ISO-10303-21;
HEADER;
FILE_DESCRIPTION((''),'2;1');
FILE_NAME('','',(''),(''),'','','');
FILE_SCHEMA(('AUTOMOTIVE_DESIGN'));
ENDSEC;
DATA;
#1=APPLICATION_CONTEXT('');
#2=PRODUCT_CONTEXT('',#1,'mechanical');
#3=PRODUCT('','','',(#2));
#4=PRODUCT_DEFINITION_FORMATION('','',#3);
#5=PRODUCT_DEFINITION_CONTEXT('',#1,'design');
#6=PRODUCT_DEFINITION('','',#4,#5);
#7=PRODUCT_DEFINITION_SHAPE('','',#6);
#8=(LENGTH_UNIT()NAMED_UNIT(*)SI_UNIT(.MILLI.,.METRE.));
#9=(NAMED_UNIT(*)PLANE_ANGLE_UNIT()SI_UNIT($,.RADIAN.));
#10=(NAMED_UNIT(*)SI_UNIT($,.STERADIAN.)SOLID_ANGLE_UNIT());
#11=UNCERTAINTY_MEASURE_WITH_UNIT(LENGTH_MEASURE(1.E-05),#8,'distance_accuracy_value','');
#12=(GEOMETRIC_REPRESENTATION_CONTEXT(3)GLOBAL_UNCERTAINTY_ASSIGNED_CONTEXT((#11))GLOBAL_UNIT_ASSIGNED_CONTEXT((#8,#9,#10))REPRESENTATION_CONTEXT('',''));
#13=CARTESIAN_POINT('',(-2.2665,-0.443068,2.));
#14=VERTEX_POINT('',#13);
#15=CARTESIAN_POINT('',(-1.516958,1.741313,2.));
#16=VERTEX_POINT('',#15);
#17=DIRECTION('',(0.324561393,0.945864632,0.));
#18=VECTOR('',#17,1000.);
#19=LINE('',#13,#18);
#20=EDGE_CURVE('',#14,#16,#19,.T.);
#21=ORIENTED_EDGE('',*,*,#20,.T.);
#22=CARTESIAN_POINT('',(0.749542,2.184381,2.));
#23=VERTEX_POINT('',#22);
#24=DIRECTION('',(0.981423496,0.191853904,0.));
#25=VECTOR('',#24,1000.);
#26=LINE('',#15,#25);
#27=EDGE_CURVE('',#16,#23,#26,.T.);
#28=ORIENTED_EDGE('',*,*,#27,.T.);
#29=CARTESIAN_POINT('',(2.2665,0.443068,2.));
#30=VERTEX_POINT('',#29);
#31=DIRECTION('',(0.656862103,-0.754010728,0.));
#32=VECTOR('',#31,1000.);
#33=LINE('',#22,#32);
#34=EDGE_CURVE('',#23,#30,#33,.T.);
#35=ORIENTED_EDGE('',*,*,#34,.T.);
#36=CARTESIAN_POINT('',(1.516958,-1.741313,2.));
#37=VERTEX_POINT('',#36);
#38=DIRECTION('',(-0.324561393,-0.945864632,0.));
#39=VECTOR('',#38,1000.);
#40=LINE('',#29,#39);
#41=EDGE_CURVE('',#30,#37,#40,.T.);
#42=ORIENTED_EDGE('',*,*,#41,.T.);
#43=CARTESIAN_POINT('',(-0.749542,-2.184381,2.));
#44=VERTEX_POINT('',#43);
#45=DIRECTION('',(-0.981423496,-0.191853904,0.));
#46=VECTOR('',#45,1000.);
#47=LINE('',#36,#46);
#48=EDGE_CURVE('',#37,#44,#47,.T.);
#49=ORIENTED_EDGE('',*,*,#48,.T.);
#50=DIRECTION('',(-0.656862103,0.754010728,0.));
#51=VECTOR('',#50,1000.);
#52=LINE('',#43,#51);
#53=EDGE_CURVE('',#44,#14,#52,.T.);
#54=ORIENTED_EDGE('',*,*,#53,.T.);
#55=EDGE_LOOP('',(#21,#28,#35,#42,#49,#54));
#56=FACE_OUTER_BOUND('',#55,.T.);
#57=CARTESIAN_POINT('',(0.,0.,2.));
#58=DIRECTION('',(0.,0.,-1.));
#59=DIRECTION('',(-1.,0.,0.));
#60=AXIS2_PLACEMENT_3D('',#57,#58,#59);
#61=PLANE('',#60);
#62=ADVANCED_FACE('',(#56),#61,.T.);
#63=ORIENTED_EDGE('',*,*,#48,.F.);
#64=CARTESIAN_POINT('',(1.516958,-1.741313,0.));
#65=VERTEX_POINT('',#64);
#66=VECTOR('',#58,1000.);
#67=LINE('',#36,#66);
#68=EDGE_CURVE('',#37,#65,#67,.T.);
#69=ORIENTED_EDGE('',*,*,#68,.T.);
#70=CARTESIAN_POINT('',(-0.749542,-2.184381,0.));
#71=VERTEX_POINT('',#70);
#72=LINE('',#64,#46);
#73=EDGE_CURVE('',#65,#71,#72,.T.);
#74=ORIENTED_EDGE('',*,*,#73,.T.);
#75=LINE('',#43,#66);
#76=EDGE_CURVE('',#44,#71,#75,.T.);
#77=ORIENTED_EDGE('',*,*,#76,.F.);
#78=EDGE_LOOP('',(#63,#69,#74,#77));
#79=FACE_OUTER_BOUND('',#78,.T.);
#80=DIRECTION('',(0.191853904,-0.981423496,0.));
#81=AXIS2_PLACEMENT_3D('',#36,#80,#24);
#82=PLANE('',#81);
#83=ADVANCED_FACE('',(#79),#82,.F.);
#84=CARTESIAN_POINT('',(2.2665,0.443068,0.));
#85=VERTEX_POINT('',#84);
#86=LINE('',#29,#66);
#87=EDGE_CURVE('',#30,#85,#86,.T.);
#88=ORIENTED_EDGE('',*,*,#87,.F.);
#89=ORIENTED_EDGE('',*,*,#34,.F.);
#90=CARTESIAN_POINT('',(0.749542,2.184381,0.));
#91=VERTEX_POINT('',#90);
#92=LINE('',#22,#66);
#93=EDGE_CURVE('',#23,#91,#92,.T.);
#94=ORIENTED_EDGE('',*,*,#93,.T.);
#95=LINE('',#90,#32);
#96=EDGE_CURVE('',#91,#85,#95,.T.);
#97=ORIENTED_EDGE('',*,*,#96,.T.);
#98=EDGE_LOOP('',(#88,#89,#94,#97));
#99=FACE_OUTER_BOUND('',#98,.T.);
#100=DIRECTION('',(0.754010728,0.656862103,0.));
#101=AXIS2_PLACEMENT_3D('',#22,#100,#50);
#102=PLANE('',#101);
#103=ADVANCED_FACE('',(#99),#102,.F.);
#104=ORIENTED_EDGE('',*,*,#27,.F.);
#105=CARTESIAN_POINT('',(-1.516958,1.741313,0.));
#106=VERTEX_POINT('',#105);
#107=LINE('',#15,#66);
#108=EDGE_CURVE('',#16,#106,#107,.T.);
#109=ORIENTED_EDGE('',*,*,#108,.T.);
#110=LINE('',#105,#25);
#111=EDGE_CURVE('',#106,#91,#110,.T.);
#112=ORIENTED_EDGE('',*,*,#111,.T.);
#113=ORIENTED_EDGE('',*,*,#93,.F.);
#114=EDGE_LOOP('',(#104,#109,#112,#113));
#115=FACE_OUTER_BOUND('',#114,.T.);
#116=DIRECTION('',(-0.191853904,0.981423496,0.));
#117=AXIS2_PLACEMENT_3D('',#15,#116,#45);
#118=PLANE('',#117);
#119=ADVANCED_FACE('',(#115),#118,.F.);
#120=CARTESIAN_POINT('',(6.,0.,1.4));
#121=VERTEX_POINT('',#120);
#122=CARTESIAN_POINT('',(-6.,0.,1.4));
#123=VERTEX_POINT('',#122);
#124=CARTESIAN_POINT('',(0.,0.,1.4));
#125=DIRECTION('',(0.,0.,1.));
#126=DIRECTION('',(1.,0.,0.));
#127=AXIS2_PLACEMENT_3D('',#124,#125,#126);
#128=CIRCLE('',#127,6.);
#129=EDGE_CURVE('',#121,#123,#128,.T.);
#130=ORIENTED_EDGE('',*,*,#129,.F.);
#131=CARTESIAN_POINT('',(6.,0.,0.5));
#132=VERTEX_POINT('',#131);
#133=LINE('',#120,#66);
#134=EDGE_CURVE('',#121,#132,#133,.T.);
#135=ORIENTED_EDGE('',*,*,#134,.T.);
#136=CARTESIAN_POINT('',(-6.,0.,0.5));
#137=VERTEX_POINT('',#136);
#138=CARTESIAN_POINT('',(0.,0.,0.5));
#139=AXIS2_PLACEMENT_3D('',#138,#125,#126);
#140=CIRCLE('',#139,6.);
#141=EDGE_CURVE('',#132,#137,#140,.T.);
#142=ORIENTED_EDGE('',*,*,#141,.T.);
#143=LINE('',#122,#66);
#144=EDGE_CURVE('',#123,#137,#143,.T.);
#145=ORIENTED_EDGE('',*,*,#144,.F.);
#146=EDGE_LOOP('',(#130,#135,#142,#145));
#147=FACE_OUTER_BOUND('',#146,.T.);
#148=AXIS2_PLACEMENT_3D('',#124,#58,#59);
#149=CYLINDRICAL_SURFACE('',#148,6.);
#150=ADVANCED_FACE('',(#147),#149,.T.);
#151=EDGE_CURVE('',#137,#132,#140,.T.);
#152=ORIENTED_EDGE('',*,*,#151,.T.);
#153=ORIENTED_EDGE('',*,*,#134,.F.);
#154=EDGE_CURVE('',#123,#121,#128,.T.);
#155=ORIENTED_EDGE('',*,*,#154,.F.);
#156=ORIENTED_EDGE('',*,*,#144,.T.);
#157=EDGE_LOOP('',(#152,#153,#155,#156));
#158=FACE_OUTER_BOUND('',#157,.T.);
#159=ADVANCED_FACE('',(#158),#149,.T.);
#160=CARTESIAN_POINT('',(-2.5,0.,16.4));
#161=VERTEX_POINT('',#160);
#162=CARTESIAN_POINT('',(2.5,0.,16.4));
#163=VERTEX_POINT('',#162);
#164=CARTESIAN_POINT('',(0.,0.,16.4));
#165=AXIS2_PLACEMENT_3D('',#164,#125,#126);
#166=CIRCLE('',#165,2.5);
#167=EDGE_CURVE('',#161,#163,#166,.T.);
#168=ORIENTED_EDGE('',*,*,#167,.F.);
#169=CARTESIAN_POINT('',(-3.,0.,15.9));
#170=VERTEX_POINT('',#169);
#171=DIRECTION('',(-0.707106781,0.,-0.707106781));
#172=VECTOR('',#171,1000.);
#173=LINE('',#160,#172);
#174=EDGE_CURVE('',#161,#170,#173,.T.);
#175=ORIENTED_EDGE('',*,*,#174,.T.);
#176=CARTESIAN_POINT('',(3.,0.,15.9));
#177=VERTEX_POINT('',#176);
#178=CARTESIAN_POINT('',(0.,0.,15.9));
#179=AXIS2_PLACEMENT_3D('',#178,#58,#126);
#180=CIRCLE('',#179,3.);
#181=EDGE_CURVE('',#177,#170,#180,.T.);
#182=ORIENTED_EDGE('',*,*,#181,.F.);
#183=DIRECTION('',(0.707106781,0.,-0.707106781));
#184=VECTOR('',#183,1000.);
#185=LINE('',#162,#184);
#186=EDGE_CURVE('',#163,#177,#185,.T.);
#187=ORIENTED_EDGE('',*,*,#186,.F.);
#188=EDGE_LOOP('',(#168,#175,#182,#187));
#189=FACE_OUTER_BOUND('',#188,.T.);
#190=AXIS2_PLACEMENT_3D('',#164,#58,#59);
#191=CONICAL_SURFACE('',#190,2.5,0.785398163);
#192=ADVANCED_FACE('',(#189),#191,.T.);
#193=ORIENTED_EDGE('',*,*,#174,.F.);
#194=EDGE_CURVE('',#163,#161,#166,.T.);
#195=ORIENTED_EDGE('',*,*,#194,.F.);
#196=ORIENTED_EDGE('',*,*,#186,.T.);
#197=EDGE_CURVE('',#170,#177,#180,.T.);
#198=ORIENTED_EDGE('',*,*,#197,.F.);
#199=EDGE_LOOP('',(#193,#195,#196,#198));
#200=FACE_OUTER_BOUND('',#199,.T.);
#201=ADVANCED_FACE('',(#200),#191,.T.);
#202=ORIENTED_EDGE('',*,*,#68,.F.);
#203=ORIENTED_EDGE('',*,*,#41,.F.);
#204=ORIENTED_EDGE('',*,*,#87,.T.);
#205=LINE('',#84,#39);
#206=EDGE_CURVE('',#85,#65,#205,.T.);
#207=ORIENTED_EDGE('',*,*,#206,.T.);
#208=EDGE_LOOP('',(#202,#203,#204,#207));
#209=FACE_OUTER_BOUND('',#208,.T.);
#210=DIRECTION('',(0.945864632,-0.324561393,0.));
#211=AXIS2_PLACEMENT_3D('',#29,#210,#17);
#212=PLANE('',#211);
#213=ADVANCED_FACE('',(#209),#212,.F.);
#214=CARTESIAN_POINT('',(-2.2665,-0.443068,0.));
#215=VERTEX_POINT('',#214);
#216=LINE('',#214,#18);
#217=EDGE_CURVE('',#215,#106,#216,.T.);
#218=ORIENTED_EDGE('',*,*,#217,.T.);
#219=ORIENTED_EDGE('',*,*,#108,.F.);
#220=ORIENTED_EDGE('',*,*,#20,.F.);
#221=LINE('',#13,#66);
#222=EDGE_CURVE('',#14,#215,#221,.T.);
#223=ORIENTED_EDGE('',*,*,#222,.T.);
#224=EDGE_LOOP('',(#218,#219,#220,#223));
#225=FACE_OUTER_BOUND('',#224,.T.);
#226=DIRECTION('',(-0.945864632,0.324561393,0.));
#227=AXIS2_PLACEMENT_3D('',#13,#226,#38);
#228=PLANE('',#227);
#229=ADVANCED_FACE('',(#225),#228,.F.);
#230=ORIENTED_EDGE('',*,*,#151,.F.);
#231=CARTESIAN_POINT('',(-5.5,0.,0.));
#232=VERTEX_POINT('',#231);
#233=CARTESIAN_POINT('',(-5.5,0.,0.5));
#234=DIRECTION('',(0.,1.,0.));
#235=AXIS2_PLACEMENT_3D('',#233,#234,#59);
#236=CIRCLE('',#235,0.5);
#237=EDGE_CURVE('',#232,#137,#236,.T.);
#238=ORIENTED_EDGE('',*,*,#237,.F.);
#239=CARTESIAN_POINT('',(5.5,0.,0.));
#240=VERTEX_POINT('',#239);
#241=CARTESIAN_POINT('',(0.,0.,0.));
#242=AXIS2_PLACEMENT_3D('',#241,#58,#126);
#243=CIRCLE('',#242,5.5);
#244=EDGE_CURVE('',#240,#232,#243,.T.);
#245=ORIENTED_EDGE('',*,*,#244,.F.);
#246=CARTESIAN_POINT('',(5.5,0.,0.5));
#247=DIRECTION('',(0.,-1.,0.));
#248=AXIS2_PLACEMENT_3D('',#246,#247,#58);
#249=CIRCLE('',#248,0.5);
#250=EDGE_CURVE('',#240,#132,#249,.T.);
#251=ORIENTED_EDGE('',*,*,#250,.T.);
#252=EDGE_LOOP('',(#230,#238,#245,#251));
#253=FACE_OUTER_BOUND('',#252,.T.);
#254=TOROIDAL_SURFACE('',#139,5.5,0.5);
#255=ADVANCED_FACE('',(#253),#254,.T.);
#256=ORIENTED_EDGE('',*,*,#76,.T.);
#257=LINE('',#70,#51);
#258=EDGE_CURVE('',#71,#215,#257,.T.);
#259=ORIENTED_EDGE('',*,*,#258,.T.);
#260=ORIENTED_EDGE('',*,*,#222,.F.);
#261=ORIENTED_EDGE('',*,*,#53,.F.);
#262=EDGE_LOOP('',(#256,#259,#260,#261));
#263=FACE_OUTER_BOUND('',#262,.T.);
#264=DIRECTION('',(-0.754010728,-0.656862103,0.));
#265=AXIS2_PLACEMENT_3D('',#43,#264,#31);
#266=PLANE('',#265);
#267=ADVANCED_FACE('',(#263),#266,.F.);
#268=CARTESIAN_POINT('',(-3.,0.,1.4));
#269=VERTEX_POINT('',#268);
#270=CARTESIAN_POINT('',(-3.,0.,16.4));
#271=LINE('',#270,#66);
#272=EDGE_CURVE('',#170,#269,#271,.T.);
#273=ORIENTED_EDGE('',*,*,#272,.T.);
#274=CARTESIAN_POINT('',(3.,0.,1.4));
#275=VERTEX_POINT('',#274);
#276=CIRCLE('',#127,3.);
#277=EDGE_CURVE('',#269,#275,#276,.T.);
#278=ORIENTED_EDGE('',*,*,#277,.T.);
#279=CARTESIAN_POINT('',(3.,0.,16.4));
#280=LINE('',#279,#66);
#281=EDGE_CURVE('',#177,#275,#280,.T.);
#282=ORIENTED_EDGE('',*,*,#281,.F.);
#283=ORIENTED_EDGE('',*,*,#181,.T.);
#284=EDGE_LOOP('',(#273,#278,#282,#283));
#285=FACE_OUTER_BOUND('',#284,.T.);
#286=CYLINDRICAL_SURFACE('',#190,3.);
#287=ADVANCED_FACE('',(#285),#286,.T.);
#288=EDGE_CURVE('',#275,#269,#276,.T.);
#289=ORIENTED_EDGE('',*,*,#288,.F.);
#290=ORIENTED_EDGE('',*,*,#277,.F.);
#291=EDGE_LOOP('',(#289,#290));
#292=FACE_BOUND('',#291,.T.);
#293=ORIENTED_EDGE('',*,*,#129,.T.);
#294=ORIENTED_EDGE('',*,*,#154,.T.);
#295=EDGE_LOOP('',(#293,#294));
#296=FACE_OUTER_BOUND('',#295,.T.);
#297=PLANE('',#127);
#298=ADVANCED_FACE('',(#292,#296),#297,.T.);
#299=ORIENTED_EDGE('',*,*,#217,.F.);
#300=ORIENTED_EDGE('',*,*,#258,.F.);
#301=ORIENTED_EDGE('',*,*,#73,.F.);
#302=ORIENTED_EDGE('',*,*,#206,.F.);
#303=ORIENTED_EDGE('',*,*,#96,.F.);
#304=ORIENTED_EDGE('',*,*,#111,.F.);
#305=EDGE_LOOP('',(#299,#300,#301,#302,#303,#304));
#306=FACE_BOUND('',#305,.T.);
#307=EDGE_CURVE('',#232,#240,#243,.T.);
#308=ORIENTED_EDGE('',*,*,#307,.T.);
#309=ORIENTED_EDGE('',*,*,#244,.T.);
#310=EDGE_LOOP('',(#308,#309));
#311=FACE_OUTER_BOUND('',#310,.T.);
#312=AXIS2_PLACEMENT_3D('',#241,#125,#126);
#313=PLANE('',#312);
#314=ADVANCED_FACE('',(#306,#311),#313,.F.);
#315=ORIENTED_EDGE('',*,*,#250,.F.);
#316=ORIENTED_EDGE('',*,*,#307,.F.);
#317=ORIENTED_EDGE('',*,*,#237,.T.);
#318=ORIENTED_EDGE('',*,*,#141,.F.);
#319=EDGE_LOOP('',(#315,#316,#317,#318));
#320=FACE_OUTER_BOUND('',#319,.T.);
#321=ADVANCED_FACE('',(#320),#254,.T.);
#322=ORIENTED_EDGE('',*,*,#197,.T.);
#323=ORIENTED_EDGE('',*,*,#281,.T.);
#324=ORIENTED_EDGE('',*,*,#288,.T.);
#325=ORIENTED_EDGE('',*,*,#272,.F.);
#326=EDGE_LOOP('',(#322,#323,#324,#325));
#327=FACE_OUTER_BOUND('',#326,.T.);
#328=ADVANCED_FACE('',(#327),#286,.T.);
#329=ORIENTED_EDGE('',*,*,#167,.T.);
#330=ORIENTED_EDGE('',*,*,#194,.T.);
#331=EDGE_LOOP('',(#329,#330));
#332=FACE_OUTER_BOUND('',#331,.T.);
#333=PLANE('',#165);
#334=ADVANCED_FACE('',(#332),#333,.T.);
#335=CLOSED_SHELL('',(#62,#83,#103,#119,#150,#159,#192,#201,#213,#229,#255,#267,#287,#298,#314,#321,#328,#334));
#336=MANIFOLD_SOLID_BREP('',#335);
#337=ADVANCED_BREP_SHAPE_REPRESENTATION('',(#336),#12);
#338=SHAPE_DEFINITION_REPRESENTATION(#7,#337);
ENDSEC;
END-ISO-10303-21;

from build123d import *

# Parameters (mm, degrees)
SKETCH_1_R          = 6
EXTRUDE_1_DEPTH     = 1.4
SKETCH_2_R          = 3
EXTRUDE_2_DEPTH     = 15
FILLET_1_R          = 0.5
CUT_EXTRUDE_1_DEPTH = 2
CHAMFER_1_SIZE      = 0.5


with BuildPart() as part:
    # 草图1 → 凸台-拉伸1 (new body)
    with BuildSketch(Plane.XY):
        Circle(SKETCH_1_R)
    extrude(amount=EXTRUDE_1_DEPTH)

    # 草图2 → 凸台-拉伸2 (add)
    with BuildSketch(Plane.XY.offset(1.4)):
        Circle(SKETCH_2_R)
    extrude(amount=EXTRUDE_2_DEPTH)

    # 圆角1
    fillet_1_edges = [part.edges().sort_by_distance(p)[0] for p in [
        (-6, 0, 0),
    ]]
    fillet(fillet_1_edges, radius=FILLET_1_R)

    # 草图3 → 切除-拉伸1 (cut)
    with BuildSketch(Plane(origin=(0, 0, 0), x_dir=(-1, 0, 0), z_dir=(0, 0, -1))):
        Polygon((0.749542431, -2.184380799), (2.266500479, -0.443067613), (1.516958048, 1.741313186), (-0.749542431, 2.184380799), (-2.266500479, 0.443067613), (-1.516958048, -1.741313186), align=None)
    extrude(amount=-CUT_EXTRUDE_1_DEPTH, mode=Mode.SUBTRACT)

    # 倒角1
    chamfer_1_edges = [part.edges().sort_by_distance(p)[0] for p in [
        (-3, 0, 16.4),
    ]]
    chamfer(chamfer_1_edges, length=CHAMFER_1_SIZE)


solid = part.part
